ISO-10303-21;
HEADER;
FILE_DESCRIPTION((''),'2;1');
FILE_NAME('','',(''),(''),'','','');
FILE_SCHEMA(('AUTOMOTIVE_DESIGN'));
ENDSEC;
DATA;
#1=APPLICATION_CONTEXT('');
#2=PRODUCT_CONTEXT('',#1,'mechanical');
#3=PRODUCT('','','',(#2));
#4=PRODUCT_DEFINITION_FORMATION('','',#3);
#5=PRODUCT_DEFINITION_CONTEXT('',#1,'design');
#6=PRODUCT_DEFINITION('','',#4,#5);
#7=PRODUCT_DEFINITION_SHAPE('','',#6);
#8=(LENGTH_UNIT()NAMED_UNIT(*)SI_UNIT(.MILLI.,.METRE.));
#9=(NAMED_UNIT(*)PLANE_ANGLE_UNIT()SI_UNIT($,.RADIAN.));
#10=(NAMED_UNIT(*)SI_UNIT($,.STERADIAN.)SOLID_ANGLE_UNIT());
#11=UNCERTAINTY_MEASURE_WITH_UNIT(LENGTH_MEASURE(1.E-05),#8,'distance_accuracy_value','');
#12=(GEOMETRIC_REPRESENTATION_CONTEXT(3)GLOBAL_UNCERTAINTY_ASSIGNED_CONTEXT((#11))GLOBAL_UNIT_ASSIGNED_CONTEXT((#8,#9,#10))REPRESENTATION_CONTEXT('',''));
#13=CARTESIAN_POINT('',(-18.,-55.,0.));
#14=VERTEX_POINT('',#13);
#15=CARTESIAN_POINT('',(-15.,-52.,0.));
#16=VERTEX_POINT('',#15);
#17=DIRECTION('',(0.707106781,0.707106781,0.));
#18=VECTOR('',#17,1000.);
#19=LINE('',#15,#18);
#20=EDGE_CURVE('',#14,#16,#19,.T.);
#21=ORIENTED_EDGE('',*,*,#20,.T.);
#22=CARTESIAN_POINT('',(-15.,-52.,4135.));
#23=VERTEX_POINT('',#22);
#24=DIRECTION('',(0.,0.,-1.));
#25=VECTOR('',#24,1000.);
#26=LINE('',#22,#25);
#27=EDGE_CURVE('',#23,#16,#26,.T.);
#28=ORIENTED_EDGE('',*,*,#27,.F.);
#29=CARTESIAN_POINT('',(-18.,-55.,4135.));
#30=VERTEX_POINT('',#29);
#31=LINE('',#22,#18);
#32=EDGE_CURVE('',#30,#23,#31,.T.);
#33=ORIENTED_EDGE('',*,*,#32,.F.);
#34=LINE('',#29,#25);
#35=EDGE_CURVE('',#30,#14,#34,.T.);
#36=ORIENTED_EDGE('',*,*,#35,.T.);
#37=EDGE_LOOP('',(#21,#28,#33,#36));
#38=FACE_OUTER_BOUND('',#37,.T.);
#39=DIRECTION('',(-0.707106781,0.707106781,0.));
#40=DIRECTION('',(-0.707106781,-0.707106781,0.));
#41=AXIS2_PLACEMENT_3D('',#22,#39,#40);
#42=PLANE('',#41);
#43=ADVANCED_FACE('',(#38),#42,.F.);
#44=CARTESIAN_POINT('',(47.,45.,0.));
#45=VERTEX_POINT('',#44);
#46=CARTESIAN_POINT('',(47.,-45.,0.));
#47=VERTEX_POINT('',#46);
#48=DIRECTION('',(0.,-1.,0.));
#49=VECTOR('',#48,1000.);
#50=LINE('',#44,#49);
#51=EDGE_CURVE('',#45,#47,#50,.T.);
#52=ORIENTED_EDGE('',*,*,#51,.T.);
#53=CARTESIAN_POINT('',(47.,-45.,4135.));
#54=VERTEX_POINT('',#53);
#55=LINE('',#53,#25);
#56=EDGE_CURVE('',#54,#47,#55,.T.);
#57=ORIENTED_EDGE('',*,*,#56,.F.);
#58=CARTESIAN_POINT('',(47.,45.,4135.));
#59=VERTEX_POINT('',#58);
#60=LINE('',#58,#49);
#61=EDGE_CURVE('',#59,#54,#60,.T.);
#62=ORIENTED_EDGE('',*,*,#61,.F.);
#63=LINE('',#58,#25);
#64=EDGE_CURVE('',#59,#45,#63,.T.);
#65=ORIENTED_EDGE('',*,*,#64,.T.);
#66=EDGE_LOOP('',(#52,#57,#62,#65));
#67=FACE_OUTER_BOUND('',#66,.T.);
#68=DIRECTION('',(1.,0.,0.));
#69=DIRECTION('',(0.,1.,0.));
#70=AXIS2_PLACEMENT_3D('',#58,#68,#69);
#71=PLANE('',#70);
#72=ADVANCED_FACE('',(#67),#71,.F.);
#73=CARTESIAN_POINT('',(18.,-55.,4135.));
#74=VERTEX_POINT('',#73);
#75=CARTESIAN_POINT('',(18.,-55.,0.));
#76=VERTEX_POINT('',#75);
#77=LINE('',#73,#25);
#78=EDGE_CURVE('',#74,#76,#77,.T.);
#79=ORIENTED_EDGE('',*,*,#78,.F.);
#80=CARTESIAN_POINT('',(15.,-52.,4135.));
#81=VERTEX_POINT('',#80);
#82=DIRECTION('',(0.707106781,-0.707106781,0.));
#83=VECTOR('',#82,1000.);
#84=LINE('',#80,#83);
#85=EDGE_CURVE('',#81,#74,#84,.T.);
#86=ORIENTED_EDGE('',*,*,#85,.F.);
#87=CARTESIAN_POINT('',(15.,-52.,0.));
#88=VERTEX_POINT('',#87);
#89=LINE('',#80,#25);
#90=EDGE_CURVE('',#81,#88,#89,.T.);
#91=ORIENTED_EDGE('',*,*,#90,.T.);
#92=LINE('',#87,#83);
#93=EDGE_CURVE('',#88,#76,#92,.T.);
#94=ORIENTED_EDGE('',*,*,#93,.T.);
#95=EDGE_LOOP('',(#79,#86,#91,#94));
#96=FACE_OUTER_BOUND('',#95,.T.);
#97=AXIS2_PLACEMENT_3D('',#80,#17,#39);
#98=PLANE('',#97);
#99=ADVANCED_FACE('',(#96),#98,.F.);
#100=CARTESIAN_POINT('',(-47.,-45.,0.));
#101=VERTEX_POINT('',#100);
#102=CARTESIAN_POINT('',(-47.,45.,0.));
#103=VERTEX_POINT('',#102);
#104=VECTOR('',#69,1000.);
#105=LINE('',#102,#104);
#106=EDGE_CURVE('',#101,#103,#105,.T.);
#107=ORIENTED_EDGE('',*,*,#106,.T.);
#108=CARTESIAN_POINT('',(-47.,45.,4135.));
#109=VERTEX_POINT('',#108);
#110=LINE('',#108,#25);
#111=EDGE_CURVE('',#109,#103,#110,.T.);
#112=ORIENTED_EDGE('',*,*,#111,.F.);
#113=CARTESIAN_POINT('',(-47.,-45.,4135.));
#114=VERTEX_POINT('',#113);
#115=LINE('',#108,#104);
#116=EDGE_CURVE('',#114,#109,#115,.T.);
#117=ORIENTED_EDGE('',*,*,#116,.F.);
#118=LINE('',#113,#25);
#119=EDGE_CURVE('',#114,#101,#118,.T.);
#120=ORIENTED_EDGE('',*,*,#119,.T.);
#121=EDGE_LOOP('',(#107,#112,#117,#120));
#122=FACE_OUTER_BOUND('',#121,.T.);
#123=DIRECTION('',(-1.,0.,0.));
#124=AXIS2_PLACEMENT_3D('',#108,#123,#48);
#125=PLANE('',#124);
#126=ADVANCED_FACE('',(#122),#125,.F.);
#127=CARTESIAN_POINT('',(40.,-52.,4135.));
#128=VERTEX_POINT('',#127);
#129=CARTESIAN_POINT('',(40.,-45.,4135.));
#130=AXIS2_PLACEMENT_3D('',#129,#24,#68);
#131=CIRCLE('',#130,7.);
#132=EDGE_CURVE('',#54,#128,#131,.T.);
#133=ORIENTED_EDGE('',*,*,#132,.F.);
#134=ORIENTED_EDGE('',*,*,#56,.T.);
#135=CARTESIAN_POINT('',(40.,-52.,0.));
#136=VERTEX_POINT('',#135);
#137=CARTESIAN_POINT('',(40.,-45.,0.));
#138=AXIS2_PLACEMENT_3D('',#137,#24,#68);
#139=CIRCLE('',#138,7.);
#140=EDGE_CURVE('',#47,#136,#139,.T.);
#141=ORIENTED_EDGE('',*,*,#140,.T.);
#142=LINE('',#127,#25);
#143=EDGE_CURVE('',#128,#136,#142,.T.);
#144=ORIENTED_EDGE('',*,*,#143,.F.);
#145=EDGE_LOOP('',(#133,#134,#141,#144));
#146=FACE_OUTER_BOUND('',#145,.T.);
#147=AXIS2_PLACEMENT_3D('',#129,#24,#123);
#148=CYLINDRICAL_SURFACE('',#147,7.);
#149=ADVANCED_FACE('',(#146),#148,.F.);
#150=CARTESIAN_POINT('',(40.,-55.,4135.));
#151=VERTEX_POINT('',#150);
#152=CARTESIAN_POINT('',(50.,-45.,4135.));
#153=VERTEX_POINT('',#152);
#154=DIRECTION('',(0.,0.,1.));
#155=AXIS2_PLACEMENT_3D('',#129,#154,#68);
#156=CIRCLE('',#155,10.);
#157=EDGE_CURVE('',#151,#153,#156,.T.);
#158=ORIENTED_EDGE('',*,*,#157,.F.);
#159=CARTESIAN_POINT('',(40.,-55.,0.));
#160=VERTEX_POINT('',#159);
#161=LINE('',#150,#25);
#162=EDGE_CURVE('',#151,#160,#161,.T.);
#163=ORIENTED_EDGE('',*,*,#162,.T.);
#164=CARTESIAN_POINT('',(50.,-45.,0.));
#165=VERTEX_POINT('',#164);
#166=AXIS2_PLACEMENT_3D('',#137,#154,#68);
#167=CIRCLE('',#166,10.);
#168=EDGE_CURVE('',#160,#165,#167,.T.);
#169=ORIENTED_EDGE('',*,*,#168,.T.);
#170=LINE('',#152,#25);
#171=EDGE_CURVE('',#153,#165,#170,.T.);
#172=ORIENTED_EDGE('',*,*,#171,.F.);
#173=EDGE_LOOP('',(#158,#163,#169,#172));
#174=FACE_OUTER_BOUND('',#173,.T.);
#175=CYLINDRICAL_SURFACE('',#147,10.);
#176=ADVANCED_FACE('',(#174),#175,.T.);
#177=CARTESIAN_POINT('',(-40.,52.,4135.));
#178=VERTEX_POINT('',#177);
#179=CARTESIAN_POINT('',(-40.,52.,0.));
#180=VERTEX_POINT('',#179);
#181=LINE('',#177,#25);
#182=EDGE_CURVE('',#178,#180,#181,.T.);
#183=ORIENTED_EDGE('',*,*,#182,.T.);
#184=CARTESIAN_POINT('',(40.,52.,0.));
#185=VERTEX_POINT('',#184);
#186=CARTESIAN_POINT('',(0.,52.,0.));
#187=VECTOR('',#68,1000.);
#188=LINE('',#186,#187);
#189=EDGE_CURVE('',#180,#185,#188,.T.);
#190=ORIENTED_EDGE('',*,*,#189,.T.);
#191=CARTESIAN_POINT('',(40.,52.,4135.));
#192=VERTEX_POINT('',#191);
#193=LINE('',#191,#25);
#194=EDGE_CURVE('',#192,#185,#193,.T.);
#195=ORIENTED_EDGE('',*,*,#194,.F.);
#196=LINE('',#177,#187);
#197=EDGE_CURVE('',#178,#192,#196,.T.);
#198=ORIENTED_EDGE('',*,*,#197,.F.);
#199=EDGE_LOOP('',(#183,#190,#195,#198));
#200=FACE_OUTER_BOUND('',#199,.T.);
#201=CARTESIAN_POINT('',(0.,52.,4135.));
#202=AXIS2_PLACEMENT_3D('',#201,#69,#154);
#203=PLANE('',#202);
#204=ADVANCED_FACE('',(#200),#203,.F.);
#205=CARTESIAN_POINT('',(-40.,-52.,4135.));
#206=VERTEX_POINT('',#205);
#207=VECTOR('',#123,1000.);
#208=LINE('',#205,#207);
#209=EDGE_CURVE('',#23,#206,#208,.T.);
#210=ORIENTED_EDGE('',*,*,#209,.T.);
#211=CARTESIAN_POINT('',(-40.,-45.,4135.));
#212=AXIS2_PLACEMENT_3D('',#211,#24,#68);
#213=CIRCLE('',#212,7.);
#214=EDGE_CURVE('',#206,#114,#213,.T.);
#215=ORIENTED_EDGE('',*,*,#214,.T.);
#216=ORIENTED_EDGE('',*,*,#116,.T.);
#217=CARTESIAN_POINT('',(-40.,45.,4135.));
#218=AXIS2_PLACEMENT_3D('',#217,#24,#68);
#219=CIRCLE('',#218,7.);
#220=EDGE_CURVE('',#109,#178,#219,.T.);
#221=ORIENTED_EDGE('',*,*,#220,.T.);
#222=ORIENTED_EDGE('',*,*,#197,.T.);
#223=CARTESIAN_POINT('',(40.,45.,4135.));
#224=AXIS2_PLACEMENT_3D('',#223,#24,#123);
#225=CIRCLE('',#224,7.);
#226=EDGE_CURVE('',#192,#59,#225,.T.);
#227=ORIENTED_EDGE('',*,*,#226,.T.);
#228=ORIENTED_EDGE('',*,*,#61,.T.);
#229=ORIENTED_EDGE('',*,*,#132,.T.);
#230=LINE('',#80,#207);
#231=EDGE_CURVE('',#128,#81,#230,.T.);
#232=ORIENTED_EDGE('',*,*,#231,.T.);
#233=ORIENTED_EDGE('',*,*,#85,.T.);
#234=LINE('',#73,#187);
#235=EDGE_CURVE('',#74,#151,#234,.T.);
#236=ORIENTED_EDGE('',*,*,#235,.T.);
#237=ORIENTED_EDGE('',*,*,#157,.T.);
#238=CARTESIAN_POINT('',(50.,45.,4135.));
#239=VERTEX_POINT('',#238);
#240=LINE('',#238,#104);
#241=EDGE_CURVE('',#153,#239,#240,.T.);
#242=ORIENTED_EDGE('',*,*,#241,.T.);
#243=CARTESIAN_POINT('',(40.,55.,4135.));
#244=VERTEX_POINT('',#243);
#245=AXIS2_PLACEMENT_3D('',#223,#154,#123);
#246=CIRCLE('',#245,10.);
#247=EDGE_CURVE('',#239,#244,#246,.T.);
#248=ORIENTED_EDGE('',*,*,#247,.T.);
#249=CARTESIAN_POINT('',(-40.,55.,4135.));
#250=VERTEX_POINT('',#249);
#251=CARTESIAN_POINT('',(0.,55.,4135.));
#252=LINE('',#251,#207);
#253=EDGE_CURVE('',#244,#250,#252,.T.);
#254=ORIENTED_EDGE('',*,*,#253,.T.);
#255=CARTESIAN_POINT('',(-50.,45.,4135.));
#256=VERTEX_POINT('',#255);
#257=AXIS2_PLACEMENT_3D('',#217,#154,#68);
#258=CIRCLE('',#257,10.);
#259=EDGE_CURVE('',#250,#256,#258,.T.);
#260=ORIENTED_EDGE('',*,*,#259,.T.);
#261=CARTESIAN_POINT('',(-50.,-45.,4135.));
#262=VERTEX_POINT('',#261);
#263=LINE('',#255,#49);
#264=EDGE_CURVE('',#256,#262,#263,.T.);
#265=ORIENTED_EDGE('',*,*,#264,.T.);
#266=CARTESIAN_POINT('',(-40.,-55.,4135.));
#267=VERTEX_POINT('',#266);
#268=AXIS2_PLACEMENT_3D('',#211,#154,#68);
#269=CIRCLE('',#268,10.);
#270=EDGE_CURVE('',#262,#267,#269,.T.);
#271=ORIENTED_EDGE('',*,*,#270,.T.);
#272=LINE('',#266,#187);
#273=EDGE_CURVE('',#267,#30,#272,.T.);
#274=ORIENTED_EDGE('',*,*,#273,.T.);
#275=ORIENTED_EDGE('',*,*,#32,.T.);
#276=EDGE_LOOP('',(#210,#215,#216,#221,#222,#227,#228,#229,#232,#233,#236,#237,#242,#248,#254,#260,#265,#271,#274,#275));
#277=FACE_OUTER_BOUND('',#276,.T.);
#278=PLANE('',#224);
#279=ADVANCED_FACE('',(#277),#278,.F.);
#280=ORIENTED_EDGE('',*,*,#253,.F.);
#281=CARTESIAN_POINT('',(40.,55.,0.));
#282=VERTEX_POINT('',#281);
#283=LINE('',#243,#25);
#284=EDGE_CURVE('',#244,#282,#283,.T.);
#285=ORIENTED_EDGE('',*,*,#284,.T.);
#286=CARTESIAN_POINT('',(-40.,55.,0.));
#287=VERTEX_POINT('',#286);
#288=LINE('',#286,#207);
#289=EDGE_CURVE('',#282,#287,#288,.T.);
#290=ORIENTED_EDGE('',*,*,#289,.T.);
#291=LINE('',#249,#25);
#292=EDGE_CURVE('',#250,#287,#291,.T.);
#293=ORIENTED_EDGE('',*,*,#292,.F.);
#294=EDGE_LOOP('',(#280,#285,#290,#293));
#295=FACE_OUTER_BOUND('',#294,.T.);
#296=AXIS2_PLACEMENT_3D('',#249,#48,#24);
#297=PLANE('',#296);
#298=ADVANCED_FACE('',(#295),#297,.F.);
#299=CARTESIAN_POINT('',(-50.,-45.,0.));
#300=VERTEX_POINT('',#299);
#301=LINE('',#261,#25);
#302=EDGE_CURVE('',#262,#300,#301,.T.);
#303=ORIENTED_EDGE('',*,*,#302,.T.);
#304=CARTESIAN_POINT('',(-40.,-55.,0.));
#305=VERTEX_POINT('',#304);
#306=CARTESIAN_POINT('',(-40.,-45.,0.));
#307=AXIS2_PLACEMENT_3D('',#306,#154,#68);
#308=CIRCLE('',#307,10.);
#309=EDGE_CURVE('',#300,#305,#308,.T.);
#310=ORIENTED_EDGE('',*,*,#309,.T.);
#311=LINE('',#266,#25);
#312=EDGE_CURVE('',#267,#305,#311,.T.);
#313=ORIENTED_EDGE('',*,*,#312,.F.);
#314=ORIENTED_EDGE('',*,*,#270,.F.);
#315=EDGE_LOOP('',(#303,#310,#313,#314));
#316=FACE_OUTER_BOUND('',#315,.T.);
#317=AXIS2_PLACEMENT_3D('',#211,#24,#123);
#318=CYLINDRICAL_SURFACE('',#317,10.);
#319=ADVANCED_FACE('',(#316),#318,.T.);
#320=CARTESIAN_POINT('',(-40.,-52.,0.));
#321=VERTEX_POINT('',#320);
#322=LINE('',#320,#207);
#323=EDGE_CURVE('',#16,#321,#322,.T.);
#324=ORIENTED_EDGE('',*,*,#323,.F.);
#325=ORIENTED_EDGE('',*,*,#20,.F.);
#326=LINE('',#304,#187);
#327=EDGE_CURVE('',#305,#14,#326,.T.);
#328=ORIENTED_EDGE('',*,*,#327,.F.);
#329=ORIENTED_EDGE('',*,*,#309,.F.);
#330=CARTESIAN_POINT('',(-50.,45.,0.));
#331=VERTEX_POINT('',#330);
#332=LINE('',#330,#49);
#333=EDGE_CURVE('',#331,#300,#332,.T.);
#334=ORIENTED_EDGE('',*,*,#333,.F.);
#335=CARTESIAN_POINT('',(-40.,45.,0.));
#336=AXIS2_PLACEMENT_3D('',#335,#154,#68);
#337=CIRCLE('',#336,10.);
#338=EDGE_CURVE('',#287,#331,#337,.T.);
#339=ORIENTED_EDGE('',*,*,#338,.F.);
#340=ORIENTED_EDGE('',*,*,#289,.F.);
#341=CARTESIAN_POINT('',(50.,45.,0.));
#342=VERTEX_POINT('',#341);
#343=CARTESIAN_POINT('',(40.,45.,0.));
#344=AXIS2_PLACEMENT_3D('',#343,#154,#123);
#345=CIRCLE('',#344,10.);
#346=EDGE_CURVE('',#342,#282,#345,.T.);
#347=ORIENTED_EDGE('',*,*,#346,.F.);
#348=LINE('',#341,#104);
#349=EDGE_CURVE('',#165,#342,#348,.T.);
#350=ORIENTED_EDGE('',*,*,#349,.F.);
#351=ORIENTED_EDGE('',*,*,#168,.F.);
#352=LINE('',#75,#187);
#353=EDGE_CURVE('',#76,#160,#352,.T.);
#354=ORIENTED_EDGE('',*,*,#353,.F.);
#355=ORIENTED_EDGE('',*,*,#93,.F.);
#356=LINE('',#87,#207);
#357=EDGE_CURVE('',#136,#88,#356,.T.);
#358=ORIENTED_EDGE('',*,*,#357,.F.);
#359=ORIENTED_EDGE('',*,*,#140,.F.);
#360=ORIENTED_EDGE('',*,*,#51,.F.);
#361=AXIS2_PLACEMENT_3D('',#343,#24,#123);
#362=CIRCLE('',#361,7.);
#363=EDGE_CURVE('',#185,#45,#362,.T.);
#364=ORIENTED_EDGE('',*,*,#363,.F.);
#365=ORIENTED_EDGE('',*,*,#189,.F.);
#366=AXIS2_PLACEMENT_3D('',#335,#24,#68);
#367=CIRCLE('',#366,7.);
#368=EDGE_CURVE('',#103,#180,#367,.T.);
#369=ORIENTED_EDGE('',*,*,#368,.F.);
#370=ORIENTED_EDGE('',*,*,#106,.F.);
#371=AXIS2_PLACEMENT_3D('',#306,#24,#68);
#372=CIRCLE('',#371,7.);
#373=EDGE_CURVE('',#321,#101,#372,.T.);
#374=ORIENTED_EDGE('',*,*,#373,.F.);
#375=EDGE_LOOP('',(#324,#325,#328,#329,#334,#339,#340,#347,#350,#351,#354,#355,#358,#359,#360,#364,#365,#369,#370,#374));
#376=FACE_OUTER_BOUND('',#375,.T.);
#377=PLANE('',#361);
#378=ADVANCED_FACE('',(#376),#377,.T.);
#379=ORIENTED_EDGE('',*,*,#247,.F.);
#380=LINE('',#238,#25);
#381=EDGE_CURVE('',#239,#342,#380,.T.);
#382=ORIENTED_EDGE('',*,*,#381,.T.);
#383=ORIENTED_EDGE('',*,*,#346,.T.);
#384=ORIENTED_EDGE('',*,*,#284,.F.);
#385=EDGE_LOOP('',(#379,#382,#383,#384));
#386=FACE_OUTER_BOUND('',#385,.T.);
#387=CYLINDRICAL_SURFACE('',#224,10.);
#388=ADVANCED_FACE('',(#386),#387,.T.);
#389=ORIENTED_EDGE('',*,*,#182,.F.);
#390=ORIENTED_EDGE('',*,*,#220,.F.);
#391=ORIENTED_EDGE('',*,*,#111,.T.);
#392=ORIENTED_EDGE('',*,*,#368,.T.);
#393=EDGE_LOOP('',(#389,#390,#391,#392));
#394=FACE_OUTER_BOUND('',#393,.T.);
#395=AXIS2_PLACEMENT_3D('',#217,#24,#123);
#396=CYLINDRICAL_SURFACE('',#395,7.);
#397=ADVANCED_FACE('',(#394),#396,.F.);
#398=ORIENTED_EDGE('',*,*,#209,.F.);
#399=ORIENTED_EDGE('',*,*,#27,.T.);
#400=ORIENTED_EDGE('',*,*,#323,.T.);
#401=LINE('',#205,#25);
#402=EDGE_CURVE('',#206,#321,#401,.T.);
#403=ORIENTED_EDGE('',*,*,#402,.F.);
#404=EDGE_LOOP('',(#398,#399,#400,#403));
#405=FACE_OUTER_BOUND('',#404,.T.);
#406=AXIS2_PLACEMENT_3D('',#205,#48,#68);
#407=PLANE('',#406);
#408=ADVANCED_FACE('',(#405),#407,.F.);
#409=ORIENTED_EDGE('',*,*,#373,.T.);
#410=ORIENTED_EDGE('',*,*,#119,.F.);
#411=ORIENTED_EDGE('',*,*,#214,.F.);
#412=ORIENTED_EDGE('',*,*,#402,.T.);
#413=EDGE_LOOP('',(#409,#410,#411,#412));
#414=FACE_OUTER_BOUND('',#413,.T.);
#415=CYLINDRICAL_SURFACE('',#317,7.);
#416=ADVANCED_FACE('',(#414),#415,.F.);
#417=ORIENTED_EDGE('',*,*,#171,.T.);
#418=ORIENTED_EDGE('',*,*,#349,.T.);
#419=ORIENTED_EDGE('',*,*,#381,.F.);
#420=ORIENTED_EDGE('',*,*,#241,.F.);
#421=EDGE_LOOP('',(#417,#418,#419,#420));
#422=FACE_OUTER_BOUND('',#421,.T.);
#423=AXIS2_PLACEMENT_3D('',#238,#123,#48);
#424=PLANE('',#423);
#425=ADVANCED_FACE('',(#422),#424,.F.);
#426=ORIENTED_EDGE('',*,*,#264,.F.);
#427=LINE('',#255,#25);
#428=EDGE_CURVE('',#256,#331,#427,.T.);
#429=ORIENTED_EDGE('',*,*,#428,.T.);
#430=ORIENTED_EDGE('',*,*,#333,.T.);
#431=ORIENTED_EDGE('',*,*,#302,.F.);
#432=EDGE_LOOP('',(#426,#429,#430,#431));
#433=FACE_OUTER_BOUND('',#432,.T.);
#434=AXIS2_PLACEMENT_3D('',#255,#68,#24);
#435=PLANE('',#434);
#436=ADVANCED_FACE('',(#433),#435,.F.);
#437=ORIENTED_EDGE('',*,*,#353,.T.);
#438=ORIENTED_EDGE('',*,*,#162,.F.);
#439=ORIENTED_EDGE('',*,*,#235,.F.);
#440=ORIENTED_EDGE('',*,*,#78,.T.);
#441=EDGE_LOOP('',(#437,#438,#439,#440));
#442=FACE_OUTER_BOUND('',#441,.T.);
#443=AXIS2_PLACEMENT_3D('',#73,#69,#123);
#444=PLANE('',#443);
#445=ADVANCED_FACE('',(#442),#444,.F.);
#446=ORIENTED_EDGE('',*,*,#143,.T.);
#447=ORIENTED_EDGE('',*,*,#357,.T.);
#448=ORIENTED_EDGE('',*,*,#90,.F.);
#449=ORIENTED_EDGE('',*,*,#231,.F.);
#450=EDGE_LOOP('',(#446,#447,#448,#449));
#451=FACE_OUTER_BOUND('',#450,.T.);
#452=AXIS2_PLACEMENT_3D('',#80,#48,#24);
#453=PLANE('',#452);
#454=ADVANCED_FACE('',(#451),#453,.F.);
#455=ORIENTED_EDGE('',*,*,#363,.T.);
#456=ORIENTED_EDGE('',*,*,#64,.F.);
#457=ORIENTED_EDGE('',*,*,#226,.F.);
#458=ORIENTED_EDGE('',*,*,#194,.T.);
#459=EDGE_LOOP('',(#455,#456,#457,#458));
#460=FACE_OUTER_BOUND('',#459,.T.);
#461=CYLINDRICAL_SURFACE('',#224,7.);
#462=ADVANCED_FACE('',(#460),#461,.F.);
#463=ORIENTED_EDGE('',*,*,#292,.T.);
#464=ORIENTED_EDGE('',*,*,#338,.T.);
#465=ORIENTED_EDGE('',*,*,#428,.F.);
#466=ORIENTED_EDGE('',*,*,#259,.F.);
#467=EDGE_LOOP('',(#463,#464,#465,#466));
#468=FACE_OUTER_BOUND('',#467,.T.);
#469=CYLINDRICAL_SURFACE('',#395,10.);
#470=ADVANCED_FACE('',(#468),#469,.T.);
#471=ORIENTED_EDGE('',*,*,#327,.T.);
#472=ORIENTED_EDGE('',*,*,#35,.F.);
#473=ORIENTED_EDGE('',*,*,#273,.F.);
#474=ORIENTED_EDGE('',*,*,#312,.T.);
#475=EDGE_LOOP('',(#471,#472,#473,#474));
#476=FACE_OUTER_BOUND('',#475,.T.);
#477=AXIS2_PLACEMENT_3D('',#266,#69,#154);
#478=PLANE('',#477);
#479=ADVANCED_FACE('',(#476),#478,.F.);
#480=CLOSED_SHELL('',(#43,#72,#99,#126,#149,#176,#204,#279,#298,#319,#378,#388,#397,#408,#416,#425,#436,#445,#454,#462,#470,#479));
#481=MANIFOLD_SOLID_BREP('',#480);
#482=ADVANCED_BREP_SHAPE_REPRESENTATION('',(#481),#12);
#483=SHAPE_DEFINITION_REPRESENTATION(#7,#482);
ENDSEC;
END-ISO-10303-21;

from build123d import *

# Parameters (mm, degrees)
BOSS_EXTRUDE1_DEPTH = 4135


with BuildPart() as part:
    # Sketch1 → Boss-Extrude1 (new body)
    with BuildSketch(Plane.XY):
        with BuildLine():
            Line((-40, 55), (0, 55))
            Line((0, 55), (40, 55))
            ThreePointArc((40, 55), (47.071067812, 52.071067812), (50, 45))
            Line((50, 45), (50, -45))
            ThreePointArc((50, -45), (47.071067812, -52.071067812), (40, -55))
            Line((40, -55), (18, -55))
            Line((18, -55), (15, -52))
            Line((15, -52), (40, -52))
            ThreePointArc((40, -52), (44.949747468, -49.949747468), (47, -45))
            Line((47, -45), (47, 45))
            ThreePointArc((47, 45), (44.949747468, 49.949747468), (40, 52))
            Line((40, 52), (0, 52))
            Line((0, 52), (-40, 52))
            ThreePointArc((-40, 52), (-44.949747468, 49.949747468), (-47, 45))
            Line((-47, 45), (-47, -45))
            ThreePointArc((-47, -45), (-44.949747468, -49.949747468), (-40, -52))
            Line((-40, -52), (-15, -52))
            Line((-15, -52), (-18, -55))
            Line((-18, -55), (-40, -55))
            ThreePointArc((-40, -55), (-47.071067812, -52.071067812), (-50, -45))
            Line((-50, -45), (-50, 45))
            ThreePointArc((-50, 45), (-47.071067812, 52.071067812), (-40, 55))
        make_face()
    extrude(amount=BOSS_EXTRUDE1_DEPTH)


solid = part.part
